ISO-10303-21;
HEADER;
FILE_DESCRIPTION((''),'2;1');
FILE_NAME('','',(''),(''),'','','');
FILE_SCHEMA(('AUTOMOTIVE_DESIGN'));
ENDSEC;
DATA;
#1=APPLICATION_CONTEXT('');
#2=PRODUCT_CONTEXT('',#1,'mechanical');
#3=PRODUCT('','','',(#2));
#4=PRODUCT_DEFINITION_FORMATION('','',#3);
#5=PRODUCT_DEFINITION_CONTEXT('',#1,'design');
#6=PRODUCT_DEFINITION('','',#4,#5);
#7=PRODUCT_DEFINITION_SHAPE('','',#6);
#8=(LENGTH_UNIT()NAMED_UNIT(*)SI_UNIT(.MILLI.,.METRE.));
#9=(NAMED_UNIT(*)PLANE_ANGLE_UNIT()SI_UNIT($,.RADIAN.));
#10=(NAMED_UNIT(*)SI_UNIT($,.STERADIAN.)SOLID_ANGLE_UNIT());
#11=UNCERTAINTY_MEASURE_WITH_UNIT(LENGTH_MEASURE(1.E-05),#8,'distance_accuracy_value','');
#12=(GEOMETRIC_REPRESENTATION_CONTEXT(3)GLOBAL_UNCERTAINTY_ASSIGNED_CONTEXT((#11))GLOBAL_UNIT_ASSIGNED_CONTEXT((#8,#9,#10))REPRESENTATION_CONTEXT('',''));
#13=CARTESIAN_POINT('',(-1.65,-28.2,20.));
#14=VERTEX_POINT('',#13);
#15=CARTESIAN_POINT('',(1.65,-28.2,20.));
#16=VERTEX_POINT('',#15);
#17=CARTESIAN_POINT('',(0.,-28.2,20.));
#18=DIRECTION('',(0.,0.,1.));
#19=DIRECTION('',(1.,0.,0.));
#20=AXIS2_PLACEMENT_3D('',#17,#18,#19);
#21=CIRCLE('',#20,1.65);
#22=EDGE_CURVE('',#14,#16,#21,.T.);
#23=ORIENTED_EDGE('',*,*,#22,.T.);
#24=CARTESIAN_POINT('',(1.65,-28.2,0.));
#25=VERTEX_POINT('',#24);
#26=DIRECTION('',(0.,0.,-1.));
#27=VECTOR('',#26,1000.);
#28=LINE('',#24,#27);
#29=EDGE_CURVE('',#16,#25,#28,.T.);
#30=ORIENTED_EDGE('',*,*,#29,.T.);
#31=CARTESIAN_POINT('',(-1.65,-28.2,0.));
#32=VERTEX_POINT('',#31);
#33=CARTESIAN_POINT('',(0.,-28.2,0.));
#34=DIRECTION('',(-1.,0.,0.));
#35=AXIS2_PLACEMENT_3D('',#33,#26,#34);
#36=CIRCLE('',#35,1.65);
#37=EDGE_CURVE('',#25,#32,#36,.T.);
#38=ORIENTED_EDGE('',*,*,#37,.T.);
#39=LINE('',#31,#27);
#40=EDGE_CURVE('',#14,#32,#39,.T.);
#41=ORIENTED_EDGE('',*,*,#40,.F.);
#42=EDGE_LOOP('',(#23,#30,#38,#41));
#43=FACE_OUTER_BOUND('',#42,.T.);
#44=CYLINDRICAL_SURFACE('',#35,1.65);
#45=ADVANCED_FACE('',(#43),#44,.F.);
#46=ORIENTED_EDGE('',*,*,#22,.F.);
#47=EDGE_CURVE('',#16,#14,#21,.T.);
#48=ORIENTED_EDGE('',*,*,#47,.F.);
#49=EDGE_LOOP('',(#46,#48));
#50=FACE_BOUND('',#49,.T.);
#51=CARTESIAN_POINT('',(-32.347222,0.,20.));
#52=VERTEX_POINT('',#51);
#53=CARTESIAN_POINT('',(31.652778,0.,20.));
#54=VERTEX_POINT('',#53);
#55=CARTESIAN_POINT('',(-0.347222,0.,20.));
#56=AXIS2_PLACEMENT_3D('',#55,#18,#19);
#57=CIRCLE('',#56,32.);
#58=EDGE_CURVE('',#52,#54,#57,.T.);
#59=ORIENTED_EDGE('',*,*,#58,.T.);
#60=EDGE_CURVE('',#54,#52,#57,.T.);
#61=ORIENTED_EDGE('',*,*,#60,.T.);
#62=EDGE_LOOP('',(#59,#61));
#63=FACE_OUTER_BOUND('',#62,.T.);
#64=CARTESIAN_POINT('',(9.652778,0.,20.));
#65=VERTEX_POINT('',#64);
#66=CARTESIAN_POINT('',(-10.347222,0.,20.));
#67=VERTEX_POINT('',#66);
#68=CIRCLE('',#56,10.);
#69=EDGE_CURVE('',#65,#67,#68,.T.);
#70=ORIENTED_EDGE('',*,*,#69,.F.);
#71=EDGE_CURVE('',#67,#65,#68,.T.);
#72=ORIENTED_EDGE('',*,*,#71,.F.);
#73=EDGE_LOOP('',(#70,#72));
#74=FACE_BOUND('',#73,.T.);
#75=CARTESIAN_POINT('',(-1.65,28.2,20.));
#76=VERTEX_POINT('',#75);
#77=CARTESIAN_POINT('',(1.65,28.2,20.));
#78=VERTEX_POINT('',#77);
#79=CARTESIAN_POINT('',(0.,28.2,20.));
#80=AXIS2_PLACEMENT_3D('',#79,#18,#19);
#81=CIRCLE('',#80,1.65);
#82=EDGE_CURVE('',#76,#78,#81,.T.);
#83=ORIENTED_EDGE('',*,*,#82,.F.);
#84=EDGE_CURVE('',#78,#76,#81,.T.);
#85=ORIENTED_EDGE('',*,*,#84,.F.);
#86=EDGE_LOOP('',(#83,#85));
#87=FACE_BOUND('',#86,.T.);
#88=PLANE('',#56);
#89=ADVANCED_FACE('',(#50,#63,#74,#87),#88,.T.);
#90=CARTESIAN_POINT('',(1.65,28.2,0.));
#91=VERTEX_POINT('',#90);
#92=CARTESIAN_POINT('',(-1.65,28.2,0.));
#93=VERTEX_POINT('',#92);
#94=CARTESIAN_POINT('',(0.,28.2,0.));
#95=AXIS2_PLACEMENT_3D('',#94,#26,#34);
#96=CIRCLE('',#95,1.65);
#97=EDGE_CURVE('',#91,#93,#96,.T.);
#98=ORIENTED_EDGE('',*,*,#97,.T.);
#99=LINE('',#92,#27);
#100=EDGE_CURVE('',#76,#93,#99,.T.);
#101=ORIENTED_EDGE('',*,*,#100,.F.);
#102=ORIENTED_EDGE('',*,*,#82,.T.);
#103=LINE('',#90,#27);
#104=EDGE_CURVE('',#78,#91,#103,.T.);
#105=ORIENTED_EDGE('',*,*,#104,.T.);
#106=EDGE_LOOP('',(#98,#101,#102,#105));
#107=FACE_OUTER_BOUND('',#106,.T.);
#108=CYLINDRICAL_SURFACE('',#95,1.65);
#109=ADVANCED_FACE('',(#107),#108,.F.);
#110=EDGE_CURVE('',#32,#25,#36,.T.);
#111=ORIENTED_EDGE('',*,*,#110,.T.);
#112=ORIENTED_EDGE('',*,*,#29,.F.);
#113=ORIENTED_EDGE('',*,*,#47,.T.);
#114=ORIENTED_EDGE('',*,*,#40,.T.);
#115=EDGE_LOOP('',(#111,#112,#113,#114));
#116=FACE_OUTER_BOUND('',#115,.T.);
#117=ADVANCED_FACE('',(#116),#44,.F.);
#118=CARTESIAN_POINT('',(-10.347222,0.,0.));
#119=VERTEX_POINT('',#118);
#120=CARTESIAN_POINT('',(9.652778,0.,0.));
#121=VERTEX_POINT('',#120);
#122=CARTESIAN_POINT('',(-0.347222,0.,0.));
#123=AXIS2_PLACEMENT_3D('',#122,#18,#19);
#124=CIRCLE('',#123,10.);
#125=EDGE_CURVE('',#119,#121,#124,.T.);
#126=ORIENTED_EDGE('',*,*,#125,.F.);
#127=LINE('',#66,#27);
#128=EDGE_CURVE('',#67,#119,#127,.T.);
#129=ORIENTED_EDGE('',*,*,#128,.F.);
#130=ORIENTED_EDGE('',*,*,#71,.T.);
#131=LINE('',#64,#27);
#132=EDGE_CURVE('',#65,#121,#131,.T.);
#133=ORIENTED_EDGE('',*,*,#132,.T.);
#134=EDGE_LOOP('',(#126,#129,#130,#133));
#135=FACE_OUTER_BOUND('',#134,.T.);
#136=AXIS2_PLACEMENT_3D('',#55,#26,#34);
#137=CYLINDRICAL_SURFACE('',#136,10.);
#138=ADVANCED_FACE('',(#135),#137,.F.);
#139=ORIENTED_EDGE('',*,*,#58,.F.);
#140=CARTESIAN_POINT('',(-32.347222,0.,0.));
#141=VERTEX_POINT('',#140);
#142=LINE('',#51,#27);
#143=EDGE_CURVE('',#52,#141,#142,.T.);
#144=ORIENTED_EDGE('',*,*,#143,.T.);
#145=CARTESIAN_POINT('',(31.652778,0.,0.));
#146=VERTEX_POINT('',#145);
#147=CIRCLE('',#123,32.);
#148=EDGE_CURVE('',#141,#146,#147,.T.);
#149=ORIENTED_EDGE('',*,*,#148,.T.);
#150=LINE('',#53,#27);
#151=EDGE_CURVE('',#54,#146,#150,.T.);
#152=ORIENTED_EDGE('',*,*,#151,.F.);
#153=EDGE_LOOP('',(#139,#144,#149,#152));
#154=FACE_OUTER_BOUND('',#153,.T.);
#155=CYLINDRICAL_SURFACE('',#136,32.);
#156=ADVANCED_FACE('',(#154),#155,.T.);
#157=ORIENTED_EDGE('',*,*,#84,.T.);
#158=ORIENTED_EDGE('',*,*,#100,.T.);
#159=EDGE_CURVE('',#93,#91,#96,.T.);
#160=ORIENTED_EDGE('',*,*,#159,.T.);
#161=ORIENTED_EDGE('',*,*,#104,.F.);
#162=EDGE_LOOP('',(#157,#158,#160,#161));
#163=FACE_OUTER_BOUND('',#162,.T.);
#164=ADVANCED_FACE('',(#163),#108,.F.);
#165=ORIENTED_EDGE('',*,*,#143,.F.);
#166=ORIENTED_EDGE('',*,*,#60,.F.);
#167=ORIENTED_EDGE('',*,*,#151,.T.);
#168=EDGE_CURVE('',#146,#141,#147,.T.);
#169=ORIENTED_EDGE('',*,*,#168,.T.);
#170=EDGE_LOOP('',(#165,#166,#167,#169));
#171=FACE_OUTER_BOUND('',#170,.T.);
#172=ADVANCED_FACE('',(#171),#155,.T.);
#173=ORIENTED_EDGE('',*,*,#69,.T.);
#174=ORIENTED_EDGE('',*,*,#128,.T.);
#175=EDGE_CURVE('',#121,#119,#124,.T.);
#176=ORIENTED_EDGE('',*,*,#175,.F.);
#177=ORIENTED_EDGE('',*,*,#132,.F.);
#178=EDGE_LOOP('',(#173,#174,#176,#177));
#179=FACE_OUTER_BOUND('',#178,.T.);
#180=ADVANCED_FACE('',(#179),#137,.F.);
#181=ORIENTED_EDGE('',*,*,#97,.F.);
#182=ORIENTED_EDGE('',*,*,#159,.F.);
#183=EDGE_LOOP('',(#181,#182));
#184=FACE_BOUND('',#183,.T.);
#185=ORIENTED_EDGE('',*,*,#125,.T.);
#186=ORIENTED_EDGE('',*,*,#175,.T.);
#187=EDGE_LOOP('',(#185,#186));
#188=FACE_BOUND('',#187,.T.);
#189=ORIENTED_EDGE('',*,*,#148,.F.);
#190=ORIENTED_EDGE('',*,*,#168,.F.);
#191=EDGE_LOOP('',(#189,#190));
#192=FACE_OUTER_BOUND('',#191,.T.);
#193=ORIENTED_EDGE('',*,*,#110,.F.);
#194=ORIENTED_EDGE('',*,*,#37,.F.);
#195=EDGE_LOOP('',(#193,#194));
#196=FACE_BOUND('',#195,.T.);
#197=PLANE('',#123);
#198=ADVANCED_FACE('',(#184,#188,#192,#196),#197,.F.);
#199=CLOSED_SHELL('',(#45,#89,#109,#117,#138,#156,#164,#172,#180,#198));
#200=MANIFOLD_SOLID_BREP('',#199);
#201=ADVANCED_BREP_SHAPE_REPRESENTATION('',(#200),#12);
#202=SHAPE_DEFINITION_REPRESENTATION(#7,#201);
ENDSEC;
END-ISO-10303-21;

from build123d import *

# Parameters (mm, degrees)
SKETCH_1_R             = 32
SKETCH_1_R_2           = 10
EXTRUDE_1_DEPTH        = 20
HOLE_WIZARD_M4_3_D     = 3.3
HOLE_WIZARD_M4_3_DEPTH = 32.1
HOLE_WIZARD_M4_3_TIP   = 0.991420021


with BuildPart() as part:
    # 草图1 → 凸台-拉伸1 (new body)
    with BuildSketch(Plane.XY):
        with Locations((-0.347222222, 0)):
            Circle(SKETCH_1_R)
        with Locations((-0.347222222, 0)):
            Circle(SKETCH_1_R_2, mode=Mode.SUBTRACT)
    extrude(amount=EXTRUDE_1_DEPTH)

    # M4 螺纹孔3
    with Locations(Plane(origin=(0, 0, 0), x_dir=(-1, 0, 0), z_dir=(0, 0, -1))):
        with Locations((0, 28.2), (0, -28.2)):
            Hole(HOLE_WIZARD_M4_3_D / 2, depth=HOLE_WIZARD_M4_3_DEPTH)
            with Locations((0, 0, -(HOLE_WIZARD_M4_3_DEPTH + HOLE_WIZARD_M4_3_TIP / 2))):  # 118° drill point
                Cone(0, HOLE_WIZARD_M4_3_D / 2, HOLE_WIZARD_M4_3_TIP, mode=Mode.SUBTRACT)


solid = part.part
